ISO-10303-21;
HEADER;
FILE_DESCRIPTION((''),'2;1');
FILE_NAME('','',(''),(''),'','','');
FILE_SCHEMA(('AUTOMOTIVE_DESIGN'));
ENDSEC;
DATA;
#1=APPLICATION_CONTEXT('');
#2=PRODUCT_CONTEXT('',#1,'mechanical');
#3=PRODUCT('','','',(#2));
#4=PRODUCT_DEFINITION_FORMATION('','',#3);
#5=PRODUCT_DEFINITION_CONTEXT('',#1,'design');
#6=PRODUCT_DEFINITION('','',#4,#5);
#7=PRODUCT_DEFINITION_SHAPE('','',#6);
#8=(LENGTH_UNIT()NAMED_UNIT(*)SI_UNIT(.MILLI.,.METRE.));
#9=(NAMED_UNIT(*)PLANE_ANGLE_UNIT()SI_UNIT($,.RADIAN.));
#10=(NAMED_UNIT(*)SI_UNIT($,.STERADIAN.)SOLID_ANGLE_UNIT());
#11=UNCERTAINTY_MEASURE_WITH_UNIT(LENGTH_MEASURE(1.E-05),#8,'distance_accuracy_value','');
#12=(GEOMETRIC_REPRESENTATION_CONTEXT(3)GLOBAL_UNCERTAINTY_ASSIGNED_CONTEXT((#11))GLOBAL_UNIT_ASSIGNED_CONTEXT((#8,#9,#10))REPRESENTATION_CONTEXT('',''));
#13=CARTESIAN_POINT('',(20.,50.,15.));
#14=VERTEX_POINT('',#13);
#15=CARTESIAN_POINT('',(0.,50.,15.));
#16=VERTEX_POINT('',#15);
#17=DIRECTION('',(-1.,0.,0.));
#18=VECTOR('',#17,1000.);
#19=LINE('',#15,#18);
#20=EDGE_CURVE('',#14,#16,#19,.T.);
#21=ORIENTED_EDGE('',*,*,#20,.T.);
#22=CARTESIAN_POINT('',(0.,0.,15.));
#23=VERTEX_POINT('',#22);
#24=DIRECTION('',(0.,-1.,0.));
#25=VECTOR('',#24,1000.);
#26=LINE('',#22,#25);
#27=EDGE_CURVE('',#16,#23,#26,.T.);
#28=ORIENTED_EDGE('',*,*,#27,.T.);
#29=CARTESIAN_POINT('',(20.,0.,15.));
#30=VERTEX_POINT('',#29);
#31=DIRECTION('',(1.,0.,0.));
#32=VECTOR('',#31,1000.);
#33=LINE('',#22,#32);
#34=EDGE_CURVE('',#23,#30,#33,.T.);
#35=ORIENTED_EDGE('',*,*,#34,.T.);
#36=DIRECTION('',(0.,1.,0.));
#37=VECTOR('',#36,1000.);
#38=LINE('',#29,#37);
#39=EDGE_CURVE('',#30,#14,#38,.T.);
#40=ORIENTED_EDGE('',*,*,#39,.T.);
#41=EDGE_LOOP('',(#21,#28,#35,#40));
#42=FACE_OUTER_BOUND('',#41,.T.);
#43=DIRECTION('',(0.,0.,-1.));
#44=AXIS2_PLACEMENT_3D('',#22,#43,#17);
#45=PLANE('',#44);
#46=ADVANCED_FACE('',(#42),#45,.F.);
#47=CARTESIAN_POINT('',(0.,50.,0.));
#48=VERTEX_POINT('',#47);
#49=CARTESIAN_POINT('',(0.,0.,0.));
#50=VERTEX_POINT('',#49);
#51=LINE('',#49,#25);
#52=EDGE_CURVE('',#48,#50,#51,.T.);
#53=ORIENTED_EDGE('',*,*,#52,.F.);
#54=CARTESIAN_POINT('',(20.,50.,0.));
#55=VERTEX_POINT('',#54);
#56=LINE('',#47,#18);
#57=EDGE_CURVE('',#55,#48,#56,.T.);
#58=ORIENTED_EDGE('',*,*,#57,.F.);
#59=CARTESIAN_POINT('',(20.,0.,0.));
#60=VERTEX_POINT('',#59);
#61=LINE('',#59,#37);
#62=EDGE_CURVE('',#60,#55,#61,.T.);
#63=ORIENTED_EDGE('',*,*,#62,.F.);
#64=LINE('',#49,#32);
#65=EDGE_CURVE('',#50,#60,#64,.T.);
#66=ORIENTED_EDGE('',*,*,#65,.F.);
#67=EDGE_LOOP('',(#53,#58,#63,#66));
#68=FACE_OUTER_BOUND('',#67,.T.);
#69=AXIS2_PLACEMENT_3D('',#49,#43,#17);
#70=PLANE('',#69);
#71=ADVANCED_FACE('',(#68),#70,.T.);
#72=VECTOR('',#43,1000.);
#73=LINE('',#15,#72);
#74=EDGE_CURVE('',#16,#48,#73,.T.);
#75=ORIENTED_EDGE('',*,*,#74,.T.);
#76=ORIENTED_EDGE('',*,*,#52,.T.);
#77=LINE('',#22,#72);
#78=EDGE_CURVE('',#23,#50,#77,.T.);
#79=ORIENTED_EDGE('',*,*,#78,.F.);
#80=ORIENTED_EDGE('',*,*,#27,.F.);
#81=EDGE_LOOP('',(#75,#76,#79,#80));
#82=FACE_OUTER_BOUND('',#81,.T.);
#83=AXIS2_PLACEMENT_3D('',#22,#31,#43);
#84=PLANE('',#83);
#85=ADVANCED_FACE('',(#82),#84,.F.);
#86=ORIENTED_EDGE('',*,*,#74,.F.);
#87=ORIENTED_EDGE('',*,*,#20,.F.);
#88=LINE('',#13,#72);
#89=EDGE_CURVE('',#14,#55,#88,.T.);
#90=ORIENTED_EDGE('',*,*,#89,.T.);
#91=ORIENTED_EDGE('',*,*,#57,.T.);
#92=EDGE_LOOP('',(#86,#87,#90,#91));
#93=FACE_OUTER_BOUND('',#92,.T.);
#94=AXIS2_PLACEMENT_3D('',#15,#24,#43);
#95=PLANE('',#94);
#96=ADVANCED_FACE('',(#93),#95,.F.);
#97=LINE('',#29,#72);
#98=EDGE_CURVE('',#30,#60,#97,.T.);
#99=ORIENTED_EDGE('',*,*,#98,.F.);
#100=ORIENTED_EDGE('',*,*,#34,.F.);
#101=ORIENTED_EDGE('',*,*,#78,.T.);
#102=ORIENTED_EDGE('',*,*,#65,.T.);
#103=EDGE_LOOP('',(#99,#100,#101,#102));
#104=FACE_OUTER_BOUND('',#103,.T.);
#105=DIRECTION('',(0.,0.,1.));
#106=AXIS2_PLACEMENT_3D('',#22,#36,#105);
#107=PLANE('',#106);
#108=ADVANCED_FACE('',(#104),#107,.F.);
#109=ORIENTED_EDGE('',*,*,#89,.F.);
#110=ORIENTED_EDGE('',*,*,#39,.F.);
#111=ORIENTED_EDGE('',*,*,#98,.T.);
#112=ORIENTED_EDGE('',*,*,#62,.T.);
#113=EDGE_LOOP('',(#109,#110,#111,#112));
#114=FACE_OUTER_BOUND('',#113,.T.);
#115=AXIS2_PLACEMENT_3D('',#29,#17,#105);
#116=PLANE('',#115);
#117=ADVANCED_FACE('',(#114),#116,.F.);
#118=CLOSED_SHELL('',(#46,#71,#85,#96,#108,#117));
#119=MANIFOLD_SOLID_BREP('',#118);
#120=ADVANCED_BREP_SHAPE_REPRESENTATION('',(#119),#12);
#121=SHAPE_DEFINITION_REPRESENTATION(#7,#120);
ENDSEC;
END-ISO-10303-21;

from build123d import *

# Parameters (mm, degrees)
SKETCH1_W           = 20
SKETCH1_H           = 50
BOSS_EXTRUDE1_DEPTH = 15


with BuildPart() as part:
    # Sketch1 → Boss-Extrude1 (new body)
    with BuildSketch(Plane.XY):
        with Locations((10, 25)):
            Rectangle(SKETCH1_W, SKETCH1_H)
    extrude(amount=BOSS_EXTRUDE1_DEPTH)


solid = part.part
